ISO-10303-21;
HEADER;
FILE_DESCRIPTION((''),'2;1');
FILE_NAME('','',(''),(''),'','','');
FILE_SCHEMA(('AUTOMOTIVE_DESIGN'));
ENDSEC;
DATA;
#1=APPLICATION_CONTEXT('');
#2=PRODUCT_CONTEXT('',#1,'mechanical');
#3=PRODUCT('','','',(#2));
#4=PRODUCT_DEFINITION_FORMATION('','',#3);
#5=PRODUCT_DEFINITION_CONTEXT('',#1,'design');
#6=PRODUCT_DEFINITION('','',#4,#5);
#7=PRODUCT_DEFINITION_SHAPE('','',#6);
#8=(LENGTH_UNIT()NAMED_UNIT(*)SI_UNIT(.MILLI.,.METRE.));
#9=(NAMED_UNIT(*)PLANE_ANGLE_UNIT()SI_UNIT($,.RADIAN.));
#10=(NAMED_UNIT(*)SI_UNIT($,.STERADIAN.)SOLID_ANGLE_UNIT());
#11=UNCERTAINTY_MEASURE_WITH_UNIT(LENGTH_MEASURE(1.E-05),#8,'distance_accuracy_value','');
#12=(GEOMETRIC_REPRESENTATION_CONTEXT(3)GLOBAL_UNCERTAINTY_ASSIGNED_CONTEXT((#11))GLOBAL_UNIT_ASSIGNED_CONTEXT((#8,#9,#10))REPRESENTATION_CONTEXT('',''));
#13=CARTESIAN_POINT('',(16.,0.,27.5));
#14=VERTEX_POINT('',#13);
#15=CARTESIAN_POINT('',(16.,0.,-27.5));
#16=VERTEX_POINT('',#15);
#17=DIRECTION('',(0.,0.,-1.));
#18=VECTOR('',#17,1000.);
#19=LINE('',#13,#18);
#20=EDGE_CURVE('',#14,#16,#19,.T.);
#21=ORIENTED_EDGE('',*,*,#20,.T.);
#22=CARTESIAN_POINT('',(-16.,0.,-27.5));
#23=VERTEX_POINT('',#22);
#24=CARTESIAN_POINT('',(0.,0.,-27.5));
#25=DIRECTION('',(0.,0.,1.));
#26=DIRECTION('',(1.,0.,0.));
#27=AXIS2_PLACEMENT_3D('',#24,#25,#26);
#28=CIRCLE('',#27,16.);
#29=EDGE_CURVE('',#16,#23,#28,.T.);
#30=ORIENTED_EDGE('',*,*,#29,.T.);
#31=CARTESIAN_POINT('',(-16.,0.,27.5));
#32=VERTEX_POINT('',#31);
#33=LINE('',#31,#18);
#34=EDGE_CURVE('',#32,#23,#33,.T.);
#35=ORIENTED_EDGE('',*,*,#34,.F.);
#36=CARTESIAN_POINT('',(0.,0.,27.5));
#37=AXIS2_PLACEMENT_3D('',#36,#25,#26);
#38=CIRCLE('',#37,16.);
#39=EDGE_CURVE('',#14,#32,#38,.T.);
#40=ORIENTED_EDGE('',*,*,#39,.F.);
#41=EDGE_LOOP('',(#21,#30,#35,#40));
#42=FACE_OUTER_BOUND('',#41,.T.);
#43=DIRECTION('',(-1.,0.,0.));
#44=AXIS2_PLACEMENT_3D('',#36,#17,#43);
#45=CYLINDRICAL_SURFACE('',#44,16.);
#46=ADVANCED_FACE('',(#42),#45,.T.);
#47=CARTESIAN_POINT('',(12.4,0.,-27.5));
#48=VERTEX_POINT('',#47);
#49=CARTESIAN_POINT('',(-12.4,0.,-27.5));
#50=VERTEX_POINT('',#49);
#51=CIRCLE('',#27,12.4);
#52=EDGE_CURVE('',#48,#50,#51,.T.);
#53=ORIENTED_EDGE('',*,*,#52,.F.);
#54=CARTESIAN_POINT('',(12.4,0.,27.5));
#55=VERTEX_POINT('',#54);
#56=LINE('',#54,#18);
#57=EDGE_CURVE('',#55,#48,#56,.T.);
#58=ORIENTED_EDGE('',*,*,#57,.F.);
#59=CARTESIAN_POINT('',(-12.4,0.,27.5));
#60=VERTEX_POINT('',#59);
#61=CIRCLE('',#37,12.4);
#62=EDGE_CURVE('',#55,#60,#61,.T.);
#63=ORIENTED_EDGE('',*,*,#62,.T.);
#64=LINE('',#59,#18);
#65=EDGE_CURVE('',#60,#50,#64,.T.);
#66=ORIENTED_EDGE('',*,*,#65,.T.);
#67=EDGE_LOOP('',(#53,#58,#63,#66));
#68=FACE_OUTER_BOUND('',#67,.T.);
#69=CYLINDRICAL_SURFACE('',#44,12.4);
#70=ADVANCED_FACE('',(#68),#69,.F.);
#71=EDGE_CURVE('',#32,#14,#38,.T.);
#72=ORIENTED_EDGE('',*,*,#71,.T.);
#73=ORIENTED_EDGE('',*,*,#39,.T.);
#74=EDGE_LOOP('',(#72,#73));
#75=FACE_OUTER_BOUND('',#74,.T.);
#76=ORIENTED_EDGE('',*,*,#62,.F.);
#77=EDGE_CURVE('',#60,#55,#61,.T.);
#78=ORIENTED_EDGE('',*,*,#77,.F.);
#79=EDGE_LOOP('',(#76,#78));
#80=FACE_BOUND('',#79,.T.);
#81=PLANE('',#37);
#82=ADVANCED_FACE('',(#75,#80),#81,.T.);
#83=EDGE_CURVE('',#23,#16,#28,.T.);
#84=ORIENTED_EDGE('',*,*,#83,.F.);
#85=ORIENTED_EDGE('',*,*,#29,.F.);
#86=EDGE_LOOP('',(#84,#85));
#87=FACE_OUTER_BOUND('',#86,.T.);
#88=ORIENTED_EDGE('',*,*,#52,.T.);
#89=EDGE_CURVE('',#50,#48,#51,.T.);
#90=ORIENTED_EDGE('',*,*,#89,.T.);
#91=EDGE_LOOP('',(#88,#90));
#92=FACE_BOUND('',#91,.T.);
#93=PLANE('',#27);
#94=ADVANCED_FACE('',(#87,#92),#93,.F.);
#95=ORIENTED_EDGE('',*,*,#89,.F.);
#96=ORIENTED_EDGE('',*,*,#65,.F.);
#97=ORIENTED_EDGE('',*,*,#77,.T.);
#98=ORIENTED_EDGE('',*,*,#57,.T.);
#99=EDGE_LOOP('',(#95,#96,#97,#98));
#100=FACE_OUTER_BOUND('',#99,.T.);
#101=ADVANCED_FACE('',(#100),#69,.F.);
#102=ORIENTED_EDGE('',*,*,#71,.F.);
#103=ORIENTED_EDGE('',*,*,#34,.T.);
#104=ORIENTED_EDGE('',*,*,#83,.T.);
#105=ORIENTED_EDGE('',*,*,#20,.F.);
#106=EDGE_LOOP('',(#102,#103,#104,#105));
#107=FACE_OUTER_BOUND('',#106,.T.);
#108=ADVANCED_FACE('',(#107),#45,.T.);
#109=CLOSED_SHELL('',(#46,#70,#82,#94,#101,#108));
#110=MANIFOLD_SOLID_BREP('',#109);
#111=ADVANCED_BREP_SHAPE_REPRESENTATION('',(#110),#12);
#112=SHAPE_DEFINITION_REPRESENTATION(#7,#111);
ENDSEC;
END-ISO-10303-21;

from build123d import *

# Parameters (mm, degrees)
SKETCH_1_R      = 16
SKETCH_1_R_2    = 12.4
EXTRUDE_1_DEPTH = 27.5


with BuildPart() as part:
    # 草图1 → 凸台-拉伸1 (new, symmetric)
    with BuildSketch(Plane.XY):
        Circle(SKETCH_1_R)
        Circle(SKETCH_1_R_2, mode=Mode.SUBTRACT)
    extrude(amount=EXTRUDE_1_DEPTH, both=True)


solid = part.part
